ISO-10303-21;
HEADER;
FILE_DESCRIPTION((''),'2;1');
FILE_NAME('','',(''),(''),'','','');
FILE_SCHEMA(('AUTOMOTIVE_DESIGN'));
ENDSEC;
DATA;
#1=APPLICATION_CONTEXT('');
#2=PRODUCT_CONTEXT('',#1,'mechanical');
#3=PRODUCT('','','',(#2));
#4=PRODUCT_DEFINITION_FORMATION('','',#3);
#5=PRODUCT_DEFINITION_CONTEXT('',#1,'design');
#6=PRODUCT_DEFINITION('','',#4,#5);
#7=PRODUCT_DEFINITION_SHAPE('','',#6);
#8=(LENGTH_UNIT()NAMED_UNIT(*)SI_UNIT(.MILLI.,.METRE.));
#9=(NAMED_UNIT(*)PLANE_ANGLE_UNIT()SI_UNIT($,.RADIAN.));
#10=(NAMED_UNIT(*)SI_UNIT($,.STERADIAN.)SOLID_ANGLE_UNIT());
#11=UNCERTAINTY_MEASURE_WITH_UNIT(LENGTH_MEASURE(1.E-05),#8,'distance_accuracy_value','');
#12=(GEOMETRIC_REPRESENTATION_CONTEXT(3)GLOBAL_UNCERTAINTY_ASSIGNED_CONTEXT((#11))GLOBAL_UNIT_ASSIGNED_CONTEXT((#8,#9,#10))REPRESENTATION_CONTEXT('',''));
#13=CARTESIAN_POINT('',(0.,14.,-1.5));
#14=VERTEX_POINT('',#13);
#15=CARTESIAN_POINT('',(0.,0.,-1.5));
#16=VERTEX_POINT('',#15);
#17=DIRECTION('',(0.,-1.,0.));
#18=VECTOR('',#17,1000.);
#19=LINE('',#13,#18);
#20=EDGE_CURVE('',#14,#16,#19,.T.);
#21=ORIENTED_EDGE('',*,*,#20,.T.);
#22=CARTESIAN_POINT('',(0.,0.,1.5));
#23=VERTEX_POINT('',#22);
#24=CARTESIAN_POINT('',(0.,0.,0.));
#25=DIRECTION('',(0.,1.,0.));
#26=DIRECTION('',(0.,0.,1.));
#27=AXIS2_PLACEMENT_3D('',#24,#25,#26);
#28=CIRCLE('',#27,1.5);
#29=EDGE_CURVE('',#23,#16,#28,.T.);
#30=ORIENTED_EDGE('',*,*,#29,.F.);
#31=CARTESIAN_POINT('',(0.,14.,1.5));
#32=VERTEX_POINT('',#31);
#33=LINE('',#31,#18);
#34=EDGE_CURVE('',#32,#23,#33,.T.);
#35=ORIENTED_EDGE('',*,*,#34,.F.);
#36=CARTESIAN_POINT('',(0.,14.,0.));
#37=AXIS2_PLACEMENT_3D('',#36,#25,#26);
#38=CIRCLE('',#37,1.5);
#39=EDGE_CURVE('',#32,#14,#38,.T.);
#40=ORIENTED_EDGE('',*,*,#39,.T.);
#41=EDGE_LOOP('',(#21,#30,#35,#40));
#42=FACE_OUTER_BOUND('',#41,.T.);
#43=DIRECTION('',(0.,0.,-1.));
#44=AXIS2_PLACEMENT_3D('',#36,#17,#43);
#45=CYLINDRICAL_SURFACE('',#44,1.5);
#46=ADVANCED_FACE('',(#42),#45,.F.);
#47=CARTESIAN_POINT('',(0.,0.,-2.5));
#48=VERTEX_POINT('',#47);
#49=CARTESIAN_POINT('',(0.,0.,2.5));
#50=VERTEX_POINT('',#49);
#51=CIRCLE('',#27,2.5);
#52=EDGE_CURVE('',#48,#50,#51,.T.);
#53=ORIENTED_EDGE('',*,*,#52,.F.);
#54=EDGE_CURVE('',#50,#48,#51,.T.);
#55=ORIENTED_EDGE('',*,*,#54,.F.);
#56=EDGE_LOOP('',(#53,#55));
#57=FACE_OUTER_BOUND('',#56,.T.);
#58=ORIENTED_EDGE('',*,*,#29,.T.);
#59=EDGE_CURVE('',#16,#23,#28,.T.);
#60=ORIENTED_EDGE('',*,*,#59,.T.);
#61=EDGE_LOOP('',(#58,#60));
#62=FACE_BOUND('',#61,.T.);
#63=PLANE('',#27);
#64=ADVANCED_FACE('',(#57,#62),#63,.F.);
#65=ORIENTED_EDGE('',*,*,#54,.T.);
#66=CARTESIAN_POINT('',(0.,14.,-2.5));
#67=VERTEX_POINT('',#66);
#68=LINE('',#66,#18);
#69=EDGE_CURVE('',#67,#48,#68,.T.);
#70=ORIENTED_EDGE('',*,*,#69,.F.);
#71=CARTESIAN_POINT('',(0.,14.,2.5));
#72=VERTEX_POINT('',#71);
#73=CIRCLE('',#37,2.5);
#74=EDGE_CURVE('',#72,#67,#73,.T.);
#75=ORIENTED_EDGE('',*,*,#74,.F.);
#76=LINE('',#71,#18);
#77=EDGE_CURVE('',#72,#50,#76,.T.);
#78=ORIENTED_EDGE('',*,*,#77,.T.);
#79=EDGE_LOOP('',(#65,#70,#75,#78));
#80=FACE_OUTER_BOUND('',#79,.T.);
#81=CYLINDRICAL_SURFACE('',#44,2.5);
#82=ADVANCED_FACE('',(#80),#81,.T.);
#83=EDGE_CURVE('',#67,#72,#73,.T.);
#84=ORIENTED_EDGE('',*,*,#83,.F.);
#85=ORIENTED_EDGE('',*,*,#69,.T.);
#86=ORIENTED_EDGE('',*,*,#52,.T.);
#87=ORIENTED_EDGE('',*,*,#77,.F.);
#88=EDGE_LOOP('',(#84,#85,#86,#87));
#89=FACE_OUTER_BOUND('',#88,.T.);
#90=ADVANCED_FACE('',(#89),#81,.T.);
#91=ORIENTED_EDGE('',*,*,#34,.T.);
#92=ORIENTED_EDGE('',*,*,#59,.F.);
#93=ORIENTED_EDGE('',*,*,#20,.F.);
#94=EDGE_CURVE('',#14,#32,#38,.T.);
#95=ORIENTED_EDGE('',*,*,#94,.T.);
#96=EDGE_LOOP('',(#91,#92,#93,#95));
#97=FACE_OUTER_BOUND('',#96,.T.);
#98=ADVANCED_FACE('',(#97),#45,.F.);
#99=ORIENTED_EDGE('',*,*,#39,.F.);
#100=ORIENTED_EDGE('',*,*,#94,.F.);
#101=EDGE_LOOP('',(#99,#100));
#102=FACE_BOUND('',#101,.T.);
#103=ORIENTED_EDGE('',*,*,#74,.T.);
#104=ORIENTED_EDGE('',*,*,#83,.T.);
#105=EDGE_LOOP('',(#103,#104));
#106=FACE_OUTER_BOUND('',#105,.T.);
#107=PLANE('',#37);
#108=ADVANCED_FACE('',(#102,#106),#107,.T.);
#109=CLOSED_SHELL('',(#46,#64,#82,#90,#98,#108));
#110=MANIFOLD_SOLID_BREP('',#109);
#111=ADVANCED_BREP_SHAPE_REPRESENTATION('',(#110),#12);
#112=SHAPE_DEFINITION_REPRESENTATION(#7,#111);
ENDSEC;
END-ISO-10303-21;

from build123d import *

# Parameters (mm, degrees)
SKETCH_1_R      = 2.5
SKETCH_1_R_2    = 1.5
EXTRUDE_1_DEPTH = 14


with BuildPart() as part:
    # 草图1 → 凸台-拉伸1 (new body)
    with BuildSketch(Plane(origin=(0, 0, 0), x_dir=(1, 0, 0), z_dir=(0, 1, 0))):
        with Locations(Location((0, 0, 0), (0, 0, 270))):
            Circle(SKETCH_1_R)
        with Locations(Location((0, 0, 0), (0, 0, 270))):
            Circle(SKETCH_1_R_2, mode=Mode.SUBTRACT)
    extrude(amount=EXTRUDE_1_DEPTH)


solid = part.part
